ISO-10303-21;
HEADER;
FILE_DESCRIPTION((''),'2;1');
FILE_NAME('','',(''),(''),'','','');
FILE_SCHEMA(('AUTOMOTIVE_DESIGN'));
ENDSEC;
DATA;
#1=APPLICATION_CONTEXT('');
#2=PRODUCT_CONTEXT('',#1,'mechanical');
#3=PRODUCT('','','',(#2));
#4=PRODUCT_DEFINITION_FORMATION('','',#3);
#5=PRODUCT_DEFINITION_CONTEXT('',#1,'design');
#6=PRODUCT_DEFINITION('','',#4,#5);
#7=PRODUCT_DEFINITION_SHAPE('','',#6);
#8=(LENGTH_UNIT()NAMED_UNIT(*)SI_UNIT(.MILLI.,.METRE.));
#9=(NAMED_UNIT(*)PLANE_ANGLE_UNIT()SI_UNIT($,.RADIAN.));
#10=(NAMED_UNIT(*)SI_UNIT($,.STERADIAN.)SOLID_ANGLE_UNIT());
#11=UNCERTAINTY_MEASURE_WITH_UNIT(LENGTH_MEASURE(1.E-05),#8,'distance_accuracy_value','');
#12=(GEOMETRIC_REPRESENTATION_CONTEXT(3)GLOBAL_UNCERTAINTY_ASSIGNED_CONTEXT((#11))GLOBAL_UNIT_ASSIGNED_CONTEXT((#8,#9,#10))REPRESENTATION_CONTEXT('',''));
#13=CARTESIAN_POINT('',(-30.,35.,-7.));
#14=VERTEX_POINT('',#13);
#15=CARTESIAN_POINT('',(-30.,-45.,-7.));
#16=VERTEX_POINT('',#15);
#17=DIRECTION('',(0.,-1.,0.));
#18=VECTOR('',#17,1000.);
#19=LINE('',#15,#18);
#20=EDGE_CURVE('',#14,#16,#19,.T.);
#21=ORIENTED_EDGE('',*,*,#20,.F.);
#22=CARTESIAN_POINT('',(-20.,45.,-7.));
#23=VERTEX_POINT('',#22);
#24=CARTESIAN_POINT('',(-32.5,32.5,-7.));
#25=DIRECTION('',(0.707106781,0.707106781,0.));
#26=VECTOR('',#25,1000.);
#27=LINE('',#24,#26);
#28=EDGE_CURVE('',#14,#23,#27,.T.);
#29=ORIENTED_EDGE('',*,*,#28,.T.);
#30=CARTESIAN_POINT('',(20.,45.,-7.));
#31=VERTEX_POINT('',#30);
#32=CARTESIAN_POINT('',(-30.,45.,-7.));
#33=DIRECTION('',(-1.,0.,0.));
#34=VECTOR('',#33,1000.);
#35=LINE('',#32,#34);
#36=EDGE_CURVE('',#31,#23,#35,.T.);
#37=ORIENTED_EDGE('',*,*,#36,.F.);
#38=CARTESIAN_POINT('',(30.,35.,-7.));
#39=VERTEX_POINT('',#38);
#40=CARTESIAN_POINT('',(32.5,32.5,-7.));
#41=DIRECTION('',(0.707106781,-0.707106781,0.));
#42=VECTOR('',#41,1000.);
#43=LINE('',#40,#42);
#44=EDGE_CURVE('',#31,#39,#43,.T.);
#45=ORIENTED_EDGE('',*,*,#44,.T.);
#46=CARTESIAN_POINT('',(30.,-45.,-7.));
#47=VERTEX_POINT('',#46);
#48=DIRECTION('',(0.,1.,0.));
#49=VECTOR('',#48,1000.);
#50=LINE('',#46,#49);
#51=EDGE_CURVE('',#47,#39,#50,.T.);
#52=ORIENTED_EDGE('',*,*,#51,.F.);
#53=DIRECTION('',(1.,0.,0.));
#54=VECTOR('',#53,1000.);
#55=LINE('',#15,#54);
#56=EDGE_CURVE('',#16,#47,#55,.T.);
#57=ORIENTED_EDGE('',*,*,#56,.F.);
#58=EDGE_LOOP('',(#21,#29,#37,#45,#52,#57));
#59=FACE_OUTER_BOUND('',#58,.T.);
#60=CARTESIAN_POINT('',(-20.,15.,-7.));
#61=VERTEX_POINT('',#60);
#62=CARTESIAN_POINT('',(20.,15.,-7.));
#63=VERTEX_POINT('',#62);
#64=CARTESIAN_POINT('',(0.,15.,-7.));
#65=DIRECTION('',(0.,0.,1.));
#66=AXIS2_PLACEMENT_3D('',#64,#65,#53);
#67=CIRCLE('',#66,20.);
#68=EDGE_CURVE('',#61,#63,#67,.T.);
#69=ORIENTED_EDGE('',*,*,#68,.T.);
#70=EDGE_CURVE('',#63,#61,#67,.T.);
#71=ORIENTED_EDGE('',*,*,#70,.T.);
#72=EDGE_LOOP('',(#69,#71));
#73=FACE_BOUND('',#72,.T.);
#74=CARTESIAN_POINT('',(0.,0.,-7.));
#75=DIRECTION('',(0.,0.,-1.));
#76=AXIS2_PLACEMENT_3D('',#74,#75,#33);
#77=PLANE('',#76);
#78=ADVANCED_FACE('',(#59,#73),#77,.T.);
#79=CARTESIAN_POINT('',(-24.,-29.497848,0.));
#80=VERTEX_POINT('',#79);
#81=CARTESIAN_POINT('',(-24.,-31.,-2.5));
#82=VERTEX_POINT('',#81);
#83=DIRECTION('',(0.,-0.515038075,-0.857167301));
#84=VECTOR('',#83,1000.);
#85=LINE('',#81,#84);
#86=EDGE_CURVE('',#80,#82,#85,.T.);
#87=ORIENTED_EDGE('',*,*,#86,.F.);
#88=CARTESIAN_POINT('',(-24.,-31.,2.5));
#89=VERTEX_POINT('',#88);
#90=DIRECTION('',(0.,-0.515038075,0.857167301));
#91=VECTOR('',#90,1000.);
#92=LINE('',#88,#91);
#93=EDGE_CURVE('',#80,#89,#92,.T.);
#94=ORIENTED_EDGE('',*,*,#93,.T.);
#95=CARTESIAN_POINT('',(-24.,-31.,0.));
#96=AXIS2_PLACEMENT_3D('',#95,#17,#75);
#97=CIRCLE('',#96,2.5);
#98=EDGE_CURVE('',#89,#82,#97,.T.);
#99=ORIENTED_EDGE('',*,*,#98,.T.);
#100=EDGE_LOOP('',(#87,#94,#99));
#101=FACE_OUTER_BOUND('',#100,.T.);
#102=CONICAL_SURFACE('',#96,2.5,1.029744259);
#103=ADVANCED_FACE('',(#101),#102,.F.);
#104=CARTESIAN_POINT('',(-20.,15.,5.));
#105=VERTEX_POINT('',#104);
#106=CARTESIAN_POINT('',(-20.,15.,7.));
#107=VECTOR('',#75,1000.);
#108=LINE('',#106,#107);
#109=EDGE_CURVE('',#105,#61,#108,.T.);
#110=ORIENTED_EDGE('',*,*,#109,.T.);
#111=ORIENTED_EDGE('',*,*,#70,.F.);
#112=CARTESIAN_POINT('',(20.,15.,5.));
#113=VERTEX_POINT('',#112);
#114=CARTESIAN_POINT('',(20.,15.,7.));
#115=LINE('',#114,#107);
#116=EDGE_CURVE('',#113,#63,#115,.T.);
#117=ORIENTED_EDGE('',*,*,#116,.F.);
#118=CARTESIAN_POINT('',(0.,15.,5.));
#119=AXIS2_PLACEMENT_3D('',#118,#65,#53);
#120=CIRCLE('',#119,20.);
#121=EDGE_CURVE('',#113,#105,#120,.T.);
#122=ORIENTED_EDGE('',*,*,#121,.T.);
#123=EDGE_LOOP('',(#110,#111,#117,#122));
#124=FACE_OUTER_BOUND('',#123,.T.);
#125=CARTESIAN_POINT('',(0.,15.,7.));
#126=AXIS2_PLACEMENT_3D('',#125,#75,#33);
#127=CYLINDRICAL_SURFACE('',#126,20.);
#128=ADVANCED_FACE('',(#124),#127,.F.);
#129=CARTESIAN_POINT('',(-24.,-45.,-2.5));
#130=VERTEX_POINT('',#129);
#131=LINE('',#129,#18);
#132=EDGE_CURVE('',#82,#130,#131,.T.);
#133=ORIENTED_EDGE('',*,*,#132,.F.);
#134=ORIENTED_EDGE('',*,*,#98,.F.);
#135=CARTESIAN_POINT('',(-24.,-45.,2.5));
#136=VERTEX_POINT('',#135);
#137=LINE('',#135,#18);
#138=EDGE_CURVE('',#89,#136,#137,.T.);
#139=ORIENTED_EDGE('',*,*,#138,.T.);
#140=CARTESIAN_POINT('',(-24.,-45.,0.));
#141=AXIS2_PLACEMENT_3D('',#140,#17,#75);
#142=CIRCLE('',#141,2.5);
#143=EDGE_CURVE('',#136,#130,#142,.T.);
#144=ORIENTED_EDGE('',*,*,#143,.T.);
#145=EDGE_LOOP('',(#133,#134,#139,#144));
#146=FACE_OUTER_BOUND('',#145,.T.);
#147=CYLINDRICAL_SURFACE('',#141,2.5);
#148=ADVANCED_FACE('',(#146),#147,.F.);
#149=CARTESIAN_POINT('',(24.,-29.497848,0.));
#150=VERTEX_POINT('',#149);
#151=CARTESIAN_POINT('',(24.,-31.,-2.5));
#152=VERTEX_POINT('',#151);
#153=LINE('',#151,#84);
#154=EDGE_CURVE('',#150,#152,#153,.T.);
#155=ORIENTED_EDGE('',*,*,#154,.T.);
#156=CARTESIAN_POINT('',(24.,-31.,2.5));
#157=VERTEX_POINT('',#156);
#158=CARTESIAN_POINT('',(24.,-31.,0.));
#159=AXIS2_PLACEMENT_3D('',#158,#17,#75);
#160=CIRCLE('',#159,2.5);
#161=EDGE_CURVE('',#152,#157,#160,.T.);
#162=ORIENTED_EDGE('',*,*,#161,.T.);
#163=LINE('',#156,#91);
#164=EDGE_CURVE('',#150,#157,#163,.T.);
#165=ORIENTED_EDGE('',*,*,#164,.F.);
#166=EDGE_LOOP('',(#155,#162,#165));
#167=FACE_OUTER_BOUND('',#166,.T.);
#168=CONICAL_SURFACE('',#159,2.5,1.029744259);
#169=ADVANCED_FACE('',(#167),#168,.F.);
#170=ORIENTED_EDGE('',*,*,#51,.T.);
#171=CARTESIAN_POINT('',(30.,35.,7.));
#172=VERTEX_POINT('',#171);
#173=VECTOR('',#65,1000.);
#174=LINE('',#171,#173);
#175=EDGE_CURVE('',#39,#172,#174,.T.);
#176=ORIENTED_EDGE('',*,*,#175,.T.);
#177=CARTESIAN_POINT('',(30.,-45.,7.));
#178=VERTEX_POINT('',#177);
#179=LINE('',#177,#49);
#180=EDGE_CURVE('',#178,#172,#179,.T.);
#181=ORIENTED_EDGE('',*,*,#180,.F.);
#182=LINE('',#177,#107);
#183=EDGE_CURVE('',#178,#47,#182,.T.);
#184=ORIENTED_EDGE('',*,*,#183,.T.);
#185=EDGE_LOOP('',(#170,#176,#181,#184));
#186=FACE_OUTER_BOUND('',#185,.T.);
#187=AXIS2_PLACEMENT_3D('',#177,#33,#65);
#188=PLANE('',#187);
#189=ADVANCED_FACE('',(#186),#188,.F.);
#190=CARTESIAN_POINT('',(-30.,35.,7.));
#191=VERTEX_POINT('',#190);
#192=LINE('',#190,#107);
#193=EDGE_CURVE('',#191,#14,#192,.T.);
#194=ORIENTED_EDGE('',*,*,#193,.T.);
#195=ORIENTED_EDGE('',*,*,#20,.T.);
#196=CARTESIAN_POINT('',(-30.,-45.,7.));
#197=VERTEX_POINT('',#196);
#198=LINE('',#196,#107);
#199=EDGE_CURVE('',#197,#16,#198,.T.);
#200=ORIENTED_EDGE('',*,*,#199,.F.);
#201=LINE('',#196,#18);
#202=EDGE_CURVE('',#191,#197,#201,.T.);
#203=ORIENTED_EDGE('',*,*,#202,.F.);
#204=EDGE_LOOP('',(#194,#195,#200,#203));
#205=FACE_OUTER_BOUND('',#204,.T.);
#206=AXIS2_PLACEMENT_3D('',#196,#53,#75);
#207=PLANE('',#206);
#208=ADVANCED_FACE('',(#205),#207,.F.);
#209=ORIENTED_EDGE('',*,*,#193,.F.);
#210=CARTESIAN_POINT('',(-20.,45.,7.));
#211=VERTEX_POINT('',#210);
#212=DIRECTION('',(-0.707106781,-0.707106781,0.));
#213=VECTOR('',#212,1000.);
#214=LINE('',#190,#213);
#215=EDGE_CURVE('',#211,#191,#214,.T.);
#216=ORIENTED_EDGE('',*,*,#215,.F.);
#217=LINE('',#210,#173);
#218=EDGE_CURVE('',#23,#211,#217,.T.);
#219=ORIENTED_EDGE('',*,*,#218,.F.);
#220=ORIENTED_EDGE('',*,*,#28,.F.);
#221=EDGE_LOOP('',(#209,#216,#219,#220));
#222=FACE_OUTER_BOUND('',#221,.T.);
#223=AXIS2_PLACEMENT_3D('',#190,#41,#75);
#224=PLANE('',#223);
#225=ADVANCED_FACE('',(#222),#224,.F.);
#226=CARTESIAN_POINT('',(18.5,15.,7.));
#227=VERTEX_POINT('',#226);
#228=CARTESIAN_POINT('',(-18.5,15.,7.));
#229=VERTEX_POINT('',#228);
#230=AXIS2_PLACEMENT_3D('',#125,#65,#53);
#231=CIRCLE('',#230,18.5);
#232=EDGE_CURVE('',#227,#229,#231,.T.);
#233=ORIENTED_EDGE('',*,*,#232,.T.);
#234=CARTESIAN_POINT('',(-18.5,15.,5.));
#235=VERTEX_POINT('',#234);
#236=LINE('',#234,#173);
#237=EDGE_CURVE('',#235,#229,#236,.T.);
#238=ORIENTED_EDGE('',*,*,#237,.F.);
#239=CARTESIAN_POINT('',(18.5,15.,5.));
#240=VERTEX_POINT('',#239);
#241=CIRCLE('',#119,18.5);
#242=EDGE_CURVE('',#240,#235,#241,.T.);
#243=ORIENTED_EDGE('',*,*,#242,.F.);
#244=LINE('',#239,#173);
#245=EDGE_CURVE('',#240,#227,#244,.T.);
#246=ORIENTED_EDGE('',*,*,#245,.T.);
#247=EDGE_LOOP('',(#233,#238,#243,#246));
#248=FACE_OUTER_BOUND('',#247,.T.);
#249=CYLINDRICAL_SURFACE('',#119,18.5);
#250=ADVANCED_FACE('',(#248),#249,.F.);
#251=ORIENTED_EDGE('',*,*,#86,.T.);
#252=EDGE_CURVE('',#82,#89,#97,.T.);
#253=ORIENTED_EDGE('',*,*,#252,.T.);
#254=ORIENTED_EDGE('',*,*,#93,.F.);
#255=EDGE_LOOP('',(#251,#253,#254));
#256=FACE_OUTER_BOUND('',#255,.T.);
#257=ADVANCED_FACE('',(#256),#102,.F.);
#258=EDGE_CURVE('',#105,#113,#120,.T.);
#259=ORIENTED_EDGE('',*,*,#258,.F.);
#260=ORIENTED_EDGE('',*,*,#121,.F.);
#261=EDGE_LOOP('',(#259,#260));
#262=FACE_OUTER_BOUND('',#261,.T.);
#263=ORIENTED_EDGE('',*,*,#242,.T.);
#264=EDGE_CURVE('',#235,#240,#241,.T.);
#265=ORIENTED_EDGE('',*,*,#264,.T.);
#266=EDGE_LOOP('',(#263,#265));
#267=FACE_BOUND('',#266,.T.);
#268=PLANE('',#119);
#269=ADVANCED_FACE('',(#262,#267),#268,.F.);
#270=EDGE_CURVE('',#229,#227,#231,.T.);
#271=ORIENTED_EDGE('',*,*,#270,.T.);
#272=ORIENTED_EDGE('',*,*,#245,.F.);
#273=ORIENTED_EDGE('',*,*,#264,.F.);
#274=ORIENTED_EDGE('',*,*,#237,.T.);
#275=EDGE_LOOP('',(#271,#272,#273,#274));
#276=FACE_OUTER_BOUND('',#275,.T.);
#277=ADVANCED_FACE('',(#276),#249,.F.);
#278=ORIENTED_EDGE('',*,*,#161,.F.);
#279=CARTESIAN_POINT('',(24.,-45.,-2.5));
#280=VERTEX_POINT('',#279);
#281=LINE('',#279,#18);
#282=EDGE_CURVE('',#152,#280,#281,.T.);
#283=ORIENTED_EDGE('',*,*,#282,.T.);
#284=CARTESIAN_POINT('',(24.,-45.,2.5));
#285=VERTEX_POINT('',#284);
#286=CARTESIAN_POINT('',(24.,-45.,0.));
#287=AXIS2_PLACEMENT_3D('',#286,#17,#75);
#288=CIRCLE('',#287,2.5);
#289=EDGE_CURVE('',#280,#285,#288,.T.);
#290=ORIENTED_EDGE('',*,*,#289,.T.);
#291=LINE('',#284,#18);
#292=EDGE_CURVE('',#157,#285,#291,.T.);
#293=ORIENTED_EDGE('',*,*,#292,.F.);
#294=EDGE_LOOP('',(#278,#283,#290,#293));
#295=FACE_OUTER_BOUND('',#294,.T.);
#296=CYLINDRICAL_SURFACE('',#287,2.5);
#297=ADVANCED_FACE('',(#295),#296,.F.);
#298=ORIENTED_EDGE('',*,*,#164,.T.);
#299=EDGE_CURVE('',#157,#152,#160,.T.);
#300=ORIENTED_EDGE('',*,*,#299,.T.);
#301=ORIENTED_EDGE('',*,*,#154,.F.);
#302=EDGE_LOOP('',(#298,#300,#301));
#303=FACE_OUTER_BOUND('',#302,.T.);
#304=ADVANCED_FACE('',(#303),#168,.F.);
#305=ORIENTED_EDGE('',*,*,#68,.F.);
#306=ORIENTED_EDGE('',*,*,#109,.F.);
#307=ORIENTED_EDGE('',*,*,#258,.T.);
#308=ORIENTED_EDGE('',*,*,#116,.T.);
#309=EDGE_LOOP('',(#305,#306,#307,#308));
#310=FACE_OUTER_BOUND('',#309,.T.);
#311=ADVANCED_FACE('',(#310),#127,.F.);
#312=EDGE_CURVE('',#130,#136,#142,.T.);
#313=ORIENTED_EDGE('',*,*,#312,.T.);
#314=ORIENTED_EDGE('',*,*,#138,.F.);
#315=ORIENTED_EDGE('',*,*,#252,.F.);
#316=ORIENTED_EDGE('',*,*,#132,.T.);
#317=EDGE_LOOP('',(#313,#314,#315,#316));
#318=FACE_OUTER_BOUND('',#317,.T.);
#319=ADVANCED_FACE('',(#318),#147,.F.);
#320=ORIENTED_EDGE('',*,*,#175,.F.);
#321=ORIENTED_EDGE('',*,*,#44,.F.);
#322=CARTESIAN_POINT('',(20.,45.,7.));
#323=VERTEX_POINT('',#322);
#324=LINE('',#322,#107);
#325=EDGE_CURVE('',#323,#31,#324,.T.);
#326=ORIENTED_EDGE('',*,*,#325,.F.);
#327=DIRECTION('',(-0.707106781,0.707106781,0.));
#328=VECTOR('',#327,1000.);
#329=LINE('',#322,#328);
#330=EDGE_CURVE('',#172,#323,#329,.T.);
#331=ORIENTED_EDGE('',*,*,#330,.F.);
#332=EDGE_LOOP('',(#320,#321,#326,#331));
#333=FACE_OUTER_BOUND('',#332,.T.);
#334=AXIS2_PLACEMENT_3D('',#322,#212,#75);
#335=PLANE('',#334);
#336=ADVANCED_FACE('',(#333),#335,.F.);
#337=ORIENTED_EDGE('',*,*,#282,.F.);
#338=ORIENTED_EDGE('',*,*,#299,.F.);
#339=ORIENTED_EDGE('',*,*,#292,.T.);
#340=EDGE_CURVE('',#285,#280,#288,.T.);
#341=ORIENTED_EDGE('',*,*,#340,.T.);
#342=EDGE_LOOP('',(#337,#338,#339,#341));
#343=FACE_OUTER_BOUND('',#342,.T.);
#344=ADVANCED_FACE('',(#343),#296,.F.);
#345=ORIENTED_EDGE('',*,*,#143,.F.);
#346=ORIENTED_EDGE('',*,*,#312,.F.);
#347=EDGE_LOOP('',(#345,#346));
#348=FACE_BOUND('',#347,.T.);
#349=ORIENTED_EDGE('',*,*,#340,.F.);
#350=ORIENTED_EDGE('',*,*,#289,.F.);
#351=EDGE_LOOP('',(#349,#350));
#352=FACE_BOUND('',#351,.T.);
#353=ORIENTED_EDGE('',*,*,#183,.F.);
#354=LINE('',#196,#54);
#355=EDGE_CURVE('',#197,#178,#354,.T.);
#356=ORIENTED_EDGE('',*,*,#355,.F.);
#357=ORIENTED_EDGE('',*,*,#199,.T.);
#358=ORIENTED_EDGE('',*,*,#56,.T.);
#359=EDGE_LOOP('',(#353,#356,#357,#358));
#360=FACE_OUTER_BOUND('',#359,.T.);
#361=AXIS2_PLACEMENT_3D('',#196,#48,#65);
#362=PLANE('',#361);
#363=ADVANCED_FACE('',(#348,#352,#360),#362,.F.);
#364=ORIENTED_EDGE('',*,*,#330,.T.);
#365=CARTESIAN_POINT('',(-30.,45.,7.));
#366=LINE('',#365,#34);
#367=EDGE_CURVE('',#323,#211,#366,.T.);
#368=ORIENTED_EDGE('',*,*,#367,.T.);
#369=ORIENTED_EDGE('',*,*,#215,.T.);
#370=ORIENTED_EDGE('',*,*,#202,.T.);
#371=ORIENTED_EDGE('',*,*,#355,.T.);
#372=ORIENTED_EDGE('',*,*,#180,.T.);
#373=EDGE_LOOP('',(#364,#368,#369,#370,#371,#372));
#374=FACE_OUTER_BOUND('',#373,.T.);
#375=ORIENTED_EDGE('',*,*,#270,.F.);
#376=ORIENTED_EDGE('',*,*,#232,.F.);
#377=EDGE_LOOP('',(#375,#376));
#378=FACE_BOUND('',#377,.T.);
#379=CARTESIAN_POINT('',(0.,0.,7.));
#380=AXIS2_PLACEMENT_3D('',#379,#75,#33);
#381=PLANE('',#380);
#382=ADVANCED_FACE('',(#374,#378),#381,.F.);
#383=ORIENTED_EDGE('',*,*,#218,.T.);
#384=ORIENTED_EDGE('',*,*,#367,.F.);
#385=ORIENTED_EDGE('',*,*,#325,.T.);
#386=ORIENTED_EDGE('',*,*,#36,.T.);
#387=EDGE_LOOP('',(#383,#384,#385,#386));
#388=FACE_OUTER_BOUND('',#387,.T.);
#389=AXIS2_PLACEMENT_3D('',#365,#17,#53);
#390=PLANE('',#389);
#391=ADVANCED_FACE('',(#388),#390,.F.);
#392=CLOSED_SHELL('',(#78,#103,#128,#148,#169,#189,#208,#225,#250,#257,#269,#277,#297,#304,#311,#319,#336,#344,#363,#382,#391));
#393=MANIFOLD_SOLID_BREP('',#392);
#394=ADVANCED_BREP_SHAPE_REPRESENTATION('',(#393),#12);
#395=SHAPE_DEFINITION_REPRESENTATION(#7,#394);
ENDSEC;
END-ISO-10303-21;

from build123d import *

# Parameters (mm, degrees)
SKETCH_1_W             = 60
SKETCH_1_H             = 90
SKETCH_1_R             = 20
EXTRUDE_1_DEPTH        = 7
EXTRUDE_START          = -2
SKETCH_2_R             = 20
SKETCH_2_R_2           = 18.5
EXTRUDE_2_DEPTH        = 2
CHAMFER_1_SIZE         = 10
HOLE_WIZARD_M6_1_D     = 5
HOLE_WIZARD_M6_1_DEPTH = 14
HOLE_WIZARD_M6_1_TIP   = 1.502151548


with BuildPart() as part:
    # 草图1 → 凸台-拉伸1 (new, symmetric)
    with BuildSketch(Plane.XY):
        Rectangle(SKETCH_1_W, SKETCH_1_H)
        with Locations((0, 15)):
            Circle(SKETCH_1_R, mode=Mode.SUBTRACT)
    extrude(amount=EXTRUDE_1_DEPTH, both=True)

    # 草图2 → 凸台-拉伸2 (add)
    with BuildSketch(Plane.XY.offset(7).offset(EXTRUDE_START)):
        with Locations((0, 15)):
            Circle(SKETCH_2_R)
        with Locations((0, 15)):
            Circle(SKETCH_2_R_2, mode=Mode.SUBTRACT)
    extrude(amount=EXTRUDE_2_DEPTH)

    # 倒角1
    chamfer_1_edges = [part.edges().sort_by_distance(p)[0] for p in [
        (-30, 45, 0),
        (30, 45, 0),
    ]]
    chamfer(chamfer_1_edges, length=CHAMFER_1_SIZE)

    # M6 螺纹孔1
    with Locations(Plane(origin=(-24, -45, 0), x_dir=(0, 0, -1), z_dir=(0, -1, 0))):
        with Locations((0, 0), (0, 48)):
            Hole(HOLE_WIZARD_M6_1_D / 2, depth=HOLE_WIZARD_M6_1_DEPTH)
            with Locations((0, 0, -(HOLE_WIZARD_M6_1_DEPTH + HOLE_WIZARD_M6_1_TIP / 2))):  # 118° drill point
                Cone(0, HOLE_WIZARD_M6_1_D / 2, HOLE_WIZARD_M6_1_TIP, mode=Mode.SUBTRACT)


solid = part.part
